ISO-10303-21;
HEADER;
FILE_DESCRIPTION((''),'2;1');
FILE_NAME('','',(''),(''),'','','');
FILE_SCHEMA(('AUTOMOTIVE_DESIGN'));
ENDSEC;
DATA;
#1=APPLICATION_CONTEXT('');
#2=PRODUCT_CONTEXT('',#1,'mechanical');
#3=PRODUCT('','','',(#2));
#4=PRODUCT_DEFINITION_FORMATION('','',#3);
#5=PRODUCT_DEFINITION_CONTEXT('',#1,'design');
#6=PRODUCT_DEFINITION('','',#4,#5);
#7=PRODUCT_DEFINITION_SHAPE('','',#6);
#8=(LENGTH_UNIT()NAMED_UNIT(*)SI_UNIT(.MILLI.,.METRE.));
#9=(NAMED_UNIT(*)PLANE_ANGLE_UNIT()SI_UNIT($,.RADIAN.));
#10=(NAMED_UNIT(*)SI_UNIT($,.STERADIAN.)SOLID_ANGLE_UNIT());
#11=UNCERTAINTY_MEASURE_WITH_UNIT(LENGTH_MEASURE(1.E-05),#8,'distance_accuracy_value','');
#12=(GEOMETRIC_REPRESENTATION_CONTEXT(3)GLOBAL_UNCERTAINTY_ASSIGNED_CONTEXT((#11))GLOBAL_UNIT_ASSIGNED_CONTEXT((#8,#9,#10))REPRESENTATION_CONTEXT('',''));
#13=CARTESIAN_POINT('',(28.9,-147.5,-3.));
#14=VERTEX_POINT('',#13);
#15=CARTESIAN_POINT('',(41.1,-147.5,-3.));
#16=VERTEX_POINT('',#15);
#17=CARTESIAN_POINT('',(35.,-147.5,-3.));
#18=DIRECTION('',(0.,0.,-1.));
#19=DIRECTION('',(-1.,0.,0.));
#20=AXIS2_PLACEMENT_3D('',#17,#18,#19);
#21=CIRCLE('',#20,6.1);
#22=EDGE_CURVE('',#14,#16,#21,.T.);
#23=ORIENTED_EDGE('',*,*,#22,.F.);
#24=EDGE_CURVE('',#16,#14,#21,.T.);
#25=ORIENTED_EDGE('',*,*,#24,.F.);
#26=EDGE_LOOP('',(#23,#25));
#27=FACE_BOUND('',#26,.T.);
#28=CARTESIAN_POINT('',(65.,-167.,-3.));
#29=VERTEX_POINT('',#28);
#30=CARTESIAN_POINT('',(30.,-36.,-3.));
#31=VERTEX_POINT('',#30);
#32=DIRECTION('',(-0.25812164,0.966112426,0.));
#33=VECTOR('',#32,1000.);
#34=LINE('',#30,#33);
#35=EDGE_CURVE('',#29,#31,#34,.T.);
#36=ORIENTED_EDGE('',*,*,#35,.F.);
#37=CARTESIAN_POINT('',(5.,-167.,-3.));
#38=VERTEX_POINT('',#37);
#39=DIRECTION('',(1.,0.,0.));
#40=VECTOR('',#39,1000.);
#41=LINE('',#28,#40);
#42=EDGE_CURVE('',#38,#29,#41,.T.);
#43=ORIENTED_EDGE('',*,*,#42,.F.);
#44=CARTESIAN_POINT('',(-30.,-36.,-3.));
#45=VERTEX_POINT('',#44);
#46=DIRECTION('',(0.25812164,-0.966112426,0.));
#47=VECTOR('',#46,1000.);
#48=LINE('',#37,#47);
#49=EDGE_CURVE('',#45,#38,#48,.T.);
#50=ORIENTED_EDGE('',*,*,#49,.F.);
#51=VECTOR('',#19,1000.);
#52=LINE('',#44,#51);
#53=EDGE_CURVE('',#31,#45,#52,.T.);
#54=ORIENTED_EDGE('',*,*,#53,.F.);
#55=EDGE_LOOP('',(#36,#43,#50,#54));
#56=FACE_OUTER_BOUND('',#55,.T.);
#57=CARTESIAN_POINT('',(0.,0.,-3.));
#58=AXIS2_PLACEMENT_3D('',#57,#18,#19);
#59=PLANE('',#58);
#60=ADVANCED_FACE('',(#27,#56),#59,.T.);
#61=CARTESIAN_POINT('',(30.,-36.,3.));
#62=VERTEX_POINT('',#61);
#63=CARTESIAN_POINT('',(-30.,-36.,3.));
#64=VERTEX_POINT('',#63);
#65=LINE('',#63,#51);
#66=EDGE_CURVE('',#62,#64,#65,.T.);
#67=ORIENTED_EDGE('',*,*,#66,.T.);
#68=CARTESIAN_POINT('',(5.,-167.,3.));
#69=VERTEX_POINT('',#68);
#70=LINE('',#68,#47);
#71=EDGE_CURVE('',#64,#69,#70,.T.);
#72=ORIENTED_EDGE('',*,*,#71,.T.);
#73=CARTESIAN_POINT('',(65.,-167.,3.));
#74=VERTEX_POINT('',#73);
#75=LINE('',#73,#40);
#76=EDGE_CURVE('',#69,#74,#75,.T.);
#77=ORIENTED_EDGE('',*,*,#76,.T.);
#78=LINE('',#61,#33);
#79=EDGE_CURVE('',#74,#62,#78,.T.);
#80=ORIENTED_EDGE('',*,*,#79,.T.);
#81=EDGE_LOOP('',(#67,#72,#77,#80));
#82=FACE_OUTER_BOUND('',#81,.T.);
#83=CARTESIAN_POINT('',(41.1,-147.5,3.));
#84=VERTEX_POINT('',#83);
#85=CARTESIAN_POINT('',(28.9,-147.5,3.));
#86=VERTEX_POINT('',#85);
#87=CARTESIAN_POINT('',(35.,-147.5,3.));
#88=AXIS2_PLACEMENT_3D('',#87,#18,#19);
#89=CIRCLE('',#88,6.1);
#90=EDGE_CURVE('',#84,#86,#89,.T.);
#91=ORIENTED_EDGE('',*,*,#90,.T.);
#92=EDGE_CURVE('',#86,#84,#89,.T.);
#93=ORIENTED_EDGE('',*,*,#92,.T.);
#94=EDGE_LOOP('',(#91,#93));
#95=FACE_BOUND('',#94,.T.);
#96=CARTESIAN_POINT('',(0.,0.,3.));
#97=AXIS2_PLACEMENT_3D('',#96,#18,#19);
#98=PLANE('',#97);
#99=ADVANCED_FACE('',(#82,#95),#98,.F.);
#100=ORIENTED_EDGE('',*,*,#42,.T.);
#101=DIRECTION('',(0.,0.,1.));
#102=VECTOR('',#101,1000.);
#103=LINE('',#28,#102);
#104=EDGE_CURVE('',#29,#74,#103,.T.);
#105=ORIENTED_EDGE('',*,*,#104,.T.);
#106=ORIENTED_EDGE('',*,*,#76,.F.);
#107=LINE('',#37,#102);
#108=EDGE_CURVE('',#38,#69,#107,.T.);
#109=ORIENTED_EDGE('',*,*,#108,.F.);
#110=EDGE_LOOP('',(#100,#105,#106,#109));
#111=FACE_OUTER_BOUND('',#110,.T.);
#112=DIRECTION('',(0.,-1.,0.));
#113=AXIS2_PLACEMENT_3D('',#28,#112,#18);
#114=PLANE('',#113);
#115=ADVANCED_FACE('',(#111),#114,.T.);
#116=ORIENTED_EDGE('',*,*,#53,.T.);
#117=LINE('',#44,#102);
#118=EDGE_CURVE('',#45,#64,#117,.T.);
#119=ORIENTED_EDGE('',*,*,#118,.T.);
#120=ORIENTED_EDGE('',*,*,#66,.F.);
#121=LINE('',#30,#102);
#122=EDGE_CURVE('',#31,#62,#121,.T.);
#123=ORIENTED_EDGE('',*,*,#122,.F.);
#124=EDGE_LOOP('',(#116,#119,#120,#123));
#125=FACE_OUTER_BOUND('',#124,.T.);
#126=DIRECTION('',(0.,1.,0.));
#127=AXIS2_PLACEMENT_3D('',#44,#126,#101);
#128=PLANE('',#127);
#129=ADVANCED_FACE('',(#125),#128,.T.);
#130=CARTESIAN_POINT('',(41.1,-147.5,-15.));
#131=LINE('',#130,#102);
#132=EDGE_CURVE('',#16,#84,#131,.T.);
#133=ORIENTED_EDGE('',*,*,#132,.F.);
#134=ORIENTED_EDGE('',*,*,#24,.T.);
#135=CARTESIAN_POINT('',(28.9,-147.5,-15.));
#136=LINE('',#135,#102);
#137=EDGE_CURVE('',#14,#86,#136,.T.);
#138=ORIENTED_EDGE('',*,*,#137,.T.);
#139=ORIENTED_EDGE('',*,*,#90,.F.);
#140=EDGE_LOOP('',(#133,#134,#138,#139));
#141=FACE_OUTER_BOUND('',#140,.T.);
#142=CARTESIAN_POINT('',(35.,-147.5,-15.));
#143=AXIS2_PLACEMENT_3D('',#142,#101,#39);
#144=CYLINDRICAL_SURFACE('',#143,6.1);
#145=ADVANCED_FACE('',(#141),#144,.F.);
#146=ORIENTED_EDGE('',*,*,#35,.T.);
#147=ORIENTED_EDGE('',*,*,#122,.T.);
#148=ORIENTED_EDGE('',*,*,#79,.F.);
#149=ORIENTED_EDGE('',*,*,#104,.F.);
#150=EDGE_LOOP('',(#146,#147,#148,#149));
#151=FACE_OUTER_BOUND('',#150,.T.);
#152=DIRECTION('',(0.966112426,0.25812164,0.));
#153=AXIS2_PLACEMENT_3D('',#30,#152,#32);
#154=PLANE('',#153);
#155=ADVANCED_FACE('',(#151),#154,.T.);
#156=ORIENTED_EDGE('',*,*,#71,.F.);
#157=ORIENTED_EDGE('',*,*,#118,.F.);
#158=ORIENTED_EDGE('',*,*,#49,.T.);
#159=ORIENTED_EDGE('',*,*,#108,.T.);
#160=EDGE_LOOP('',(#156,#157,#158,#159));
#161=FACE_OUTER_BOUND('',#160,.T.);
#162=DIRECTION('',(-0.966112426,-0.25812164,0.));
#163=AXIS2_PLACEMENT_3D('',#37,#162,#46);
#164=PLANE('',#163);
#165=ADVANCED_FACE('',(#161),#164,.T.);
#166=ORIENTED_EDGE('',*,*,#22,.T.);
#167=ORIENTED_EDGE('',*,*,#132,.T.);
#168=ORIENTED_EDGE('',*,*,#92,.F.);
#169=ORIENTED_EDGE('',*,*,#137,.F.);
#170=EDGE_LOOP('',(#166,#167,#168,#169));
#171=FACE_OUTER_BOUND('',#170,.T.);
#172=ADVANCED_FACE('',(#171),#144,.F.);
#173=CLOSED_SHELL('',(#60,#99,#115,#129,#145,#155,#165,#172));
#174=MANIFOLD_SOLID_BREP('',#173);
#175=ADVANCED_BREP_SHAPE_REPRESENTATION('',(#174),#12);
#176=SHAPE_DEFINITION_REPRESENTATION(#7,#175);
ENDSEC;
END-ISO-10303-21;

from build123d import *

# Parameters (mm, degrees)
EXTRUDE_1_DEPTH     = 3
SKETCH_2_R          = 6.1
CUT_EXTRUDE_1_DEPTH = 15


with BuildPart() as part:
    # 草图1 → 凸台-拉伸1 (new, symmetric)
    with BuildSketch(Plane.XY):
        Polygon((-30, -36), (30, -36), (65, -167), (5, -167), align=None)
    extrude(amount=EXTRUDE_1_DEPTH, both=True)

    # 草图2 → 切除-拉伸1 (cut, symmetric)
    with BuildSketch(Plane.XY):
        with Locations(Location((35, -147.5, 0), (0, 0, 180))):
            Circle(SKETCH_2_R)
    extrude(amount=CUT_EXTRUDE_1_DEPTH, both=True, mode=Mode.SUBTRACT)


solid = part.part
